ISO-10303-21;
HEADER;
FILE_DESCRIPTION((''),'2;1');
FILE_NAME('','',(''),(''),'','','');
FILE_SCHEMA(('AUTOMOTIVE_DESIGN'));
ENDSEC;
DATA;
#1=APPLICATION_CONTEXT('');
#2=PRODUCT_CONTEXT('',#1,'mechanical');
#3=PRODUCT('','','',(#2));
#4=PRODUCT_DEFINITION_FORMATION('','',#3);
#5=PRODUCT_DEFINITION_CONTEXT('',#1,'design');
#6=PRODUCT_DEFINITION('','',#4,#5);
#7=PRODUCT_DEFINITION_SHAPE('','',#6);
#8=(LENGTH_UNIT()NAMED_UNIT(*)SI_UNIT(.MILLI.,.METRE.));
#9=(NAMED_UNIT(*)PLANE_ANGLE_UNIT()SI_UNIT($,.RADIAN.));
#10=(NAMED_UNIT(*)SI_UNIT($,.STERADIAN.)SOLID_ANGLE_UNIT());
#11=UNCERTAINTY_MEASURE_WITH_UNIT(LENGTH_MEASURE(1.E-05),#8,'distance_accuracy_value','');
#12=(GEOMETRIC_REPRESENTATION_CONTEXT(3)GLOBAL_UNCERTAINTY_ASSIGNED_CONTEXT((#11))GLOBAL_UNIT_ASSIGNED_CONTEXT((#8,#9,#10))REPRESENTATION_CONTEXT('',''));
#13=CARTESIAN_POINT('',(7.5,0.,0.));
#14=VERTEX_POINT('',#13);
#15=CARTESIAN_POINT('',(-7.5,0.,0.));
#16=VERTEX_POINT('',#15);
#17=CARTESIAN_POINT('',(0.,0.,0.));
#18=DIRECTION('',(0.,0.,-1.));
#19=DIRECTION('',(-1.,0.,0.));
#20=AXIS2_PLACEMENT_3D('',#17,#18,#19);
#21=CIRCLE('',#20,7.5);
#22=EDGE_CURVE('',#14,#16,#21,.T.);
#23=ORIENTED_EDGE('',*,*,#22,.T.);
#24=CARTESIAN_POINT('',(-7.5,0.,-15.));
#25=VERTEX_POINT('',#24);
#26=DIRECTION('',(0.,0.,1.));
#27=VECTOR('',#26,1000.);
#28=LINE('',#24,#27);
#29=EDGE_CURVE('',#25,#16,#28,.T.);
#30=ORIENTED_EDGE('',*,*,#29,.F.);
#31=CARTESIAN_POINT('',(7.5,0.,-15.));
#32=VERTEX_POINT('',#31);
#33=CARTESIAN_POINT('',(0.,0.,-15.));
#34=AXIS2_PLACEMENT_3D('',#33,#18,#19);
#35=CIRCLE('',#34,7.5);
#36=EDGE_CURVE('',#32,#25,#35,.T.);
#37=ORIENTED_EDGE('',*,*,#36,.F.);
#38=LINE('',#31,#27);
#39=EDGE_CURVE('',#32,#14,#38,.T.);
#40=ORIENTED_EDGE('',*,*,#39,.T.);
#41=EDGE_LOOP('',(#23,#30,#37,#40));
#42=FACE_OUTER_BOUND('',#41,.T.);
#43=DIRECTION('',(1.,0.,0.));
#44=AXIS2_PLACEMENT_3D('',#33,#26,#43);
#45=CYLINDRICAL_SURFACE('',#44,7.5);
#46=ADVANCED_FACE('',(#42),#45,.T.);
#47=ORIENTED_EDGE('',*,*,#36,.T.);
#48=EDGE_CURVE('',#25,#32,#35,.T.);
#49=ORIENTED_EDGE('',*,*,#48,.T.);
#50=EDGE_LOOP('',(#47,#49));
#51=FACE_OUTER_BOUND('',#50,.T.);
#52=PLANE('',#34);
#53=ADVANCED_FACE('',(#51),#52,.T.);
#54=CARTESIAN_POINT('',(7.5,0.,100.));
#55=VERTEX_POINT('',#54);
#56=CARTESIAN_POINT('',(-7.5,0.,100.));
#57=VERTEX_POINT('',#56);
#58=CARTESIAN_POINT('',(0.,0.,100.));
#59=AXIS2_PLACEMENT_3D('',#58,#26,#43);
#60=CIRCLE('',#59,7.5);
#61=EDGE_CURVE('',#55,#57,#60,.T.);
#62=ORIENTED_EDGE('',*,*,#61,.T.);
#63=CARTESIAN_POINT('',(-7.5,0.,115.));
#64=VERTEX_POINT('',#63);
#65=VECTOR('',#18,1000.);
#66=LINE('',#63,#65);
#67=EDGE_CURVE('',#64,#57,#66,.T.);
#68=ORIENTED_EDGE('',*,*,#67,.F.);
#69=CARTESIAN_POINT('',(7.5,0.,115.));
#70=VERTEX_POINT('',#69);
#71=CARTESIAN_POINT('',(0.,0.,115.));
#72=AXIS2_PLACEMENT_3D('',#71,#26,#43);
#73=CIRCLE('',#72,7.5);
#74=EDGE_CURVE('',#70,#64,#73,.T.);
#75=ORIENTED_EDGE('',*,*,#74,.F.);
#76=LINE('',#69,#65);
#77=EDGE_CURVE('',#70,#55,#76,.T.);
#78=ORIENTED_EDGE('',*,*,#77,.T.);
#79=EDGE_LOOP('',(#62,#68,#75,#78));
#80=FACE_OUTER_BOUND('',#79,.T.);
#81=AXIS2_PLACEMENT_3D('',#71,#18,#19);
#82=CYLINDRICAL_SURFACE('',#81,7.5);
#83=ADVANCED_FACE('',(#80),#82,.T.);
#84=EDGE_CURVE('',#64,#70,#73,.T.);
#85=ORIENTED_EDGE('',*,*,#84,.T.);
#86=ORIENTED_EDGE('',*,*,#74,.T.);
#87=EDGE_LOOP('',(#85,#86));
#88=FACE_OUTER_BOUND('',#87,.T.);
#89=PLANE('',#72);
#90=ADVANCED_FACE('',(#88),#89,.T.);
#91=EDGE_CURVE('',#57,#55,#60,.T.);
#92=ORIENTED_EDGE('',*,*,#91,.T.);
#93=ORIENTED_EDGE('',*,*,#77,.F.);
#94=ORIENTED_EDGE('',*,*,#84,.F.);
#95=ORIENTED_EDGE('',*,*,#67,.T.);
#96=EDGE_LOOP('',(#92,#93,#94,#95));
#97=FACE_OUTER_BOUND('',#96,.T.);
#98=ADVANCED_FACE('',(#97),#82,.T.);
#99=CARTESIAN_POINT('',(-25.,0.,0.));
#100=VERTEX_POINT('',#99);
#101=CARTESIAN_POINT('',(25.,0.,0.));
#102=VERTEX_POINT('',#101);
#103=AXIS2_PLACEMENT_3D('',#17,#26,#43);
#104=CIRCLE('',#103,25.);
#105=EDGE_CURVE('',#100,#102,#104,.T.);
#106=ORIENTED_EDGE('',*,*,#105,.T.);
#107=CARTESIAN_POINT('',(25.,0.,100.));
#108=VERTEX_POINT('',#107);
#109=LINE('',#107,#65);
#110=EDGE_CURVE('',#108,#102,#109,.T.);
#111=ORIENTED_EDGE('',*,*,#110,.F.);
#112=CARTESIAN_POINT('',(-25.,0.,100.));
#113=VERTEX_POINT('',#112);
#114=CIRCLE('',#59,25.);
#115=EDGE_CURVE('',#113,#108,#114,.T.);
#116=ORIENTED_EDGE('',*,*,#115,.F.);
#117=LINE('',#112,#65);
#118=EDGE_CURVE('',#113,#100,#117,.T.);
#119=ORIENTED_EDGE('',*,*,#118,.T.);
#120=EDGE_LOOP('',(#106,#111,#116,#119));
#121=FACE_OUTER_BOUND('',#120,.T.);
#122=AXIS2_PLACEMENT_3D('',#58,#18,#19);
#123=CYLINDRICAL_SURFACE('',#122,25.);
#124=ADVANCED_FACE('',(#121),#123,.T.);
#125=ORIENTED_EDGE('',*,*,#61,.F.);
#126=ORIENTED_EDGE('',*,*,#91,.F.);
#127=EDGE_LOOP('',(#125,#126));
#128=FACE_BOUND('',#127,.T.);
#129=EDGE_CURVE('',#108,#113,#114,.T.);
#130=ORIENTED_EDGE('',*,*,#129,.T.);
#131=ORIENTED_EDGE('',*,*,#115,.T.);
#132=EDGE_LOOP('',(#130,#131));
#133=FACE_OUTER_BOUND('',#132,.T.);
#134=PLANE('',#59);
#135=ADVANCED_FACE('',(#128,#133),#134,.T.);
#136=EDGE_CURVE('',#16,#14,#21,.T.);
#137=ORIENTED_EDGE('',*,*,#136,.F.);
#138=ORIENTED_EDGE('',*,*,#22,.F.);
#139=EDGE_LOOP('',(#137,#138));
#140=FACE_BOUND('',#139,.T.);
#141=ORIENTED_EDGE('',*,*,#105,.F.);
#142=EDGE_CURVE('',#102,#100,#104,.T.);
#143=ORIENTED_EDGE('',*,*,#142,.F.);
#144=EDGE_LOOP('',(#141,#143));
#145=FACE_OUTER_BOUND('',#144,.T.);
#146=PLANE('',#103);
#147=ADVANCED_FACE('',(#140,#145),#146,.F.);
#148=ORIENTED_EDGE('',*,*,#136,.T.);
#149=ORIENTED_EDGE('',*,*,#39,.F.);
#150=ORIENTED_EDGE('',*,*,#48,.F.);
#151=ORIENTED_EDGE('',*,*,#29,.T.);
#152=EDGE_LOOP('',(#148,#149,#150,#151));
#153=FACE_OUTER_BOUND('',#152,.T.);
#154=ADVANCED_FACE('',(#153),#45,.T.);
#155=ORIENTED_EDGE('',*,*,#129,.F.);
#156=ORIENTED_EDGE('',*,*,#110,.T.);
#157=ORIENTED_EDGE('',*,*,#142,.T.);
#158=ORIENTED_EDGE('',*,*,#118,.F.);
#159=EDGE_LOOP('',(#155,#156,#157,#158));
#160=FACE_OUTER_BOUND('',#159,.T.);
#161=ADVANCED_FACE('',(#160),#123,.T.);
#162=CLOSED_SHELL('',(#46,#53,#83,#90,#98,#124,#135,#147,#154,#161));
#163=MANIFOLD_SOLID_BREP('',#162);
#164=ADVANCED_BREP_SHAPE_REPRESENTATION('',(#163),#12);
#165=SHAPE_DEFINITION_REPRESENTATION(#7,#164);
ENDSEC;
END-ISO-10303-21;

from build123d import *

# Parameters (mm, degrees)
SKETCH_1_R      = 25
EXTRUDE_1_DEPTH = 100
SKETCH_2_R      = 7.5
EXTRUDE_2_DEPTH = 15
EXTRUDE_START   = 15
SKETCH_3_R      = 7.5
EXTRUDE_3_DEPTH = 15


with BuildPart() as part:
    # 草图1 → 凸台-拉伸1 (new body)
    with BuildSketch(Plane.XY):
        Circle(SKETCH_1_R)
    extrude(amount=EXTRUDE_1_DEPTH)

    # 草图2 → 凸台-拉伸2 (add)
    with BuildSketch(Plane.XY.offset(100)):
        Circle(SKETCH_2_R)
    extrude(amount=EXTRUDE_2_DEPTH)

    # 草图3 → 凸台-拉伸3 (add)
    with BuildSketch(Plane(origin=(0, 0, 0), x_dir=(-1, 0, 0), z_dir=(0, 0, -1)).offset(EXTRUDE_START)):
        with Locations(Location((0, 0, 0), (0, 0, 180))):
            Circle(SKETCH_3_R)
    extrude(amount=-EXTRUDE_3_DEPTH)


solid = part.part
